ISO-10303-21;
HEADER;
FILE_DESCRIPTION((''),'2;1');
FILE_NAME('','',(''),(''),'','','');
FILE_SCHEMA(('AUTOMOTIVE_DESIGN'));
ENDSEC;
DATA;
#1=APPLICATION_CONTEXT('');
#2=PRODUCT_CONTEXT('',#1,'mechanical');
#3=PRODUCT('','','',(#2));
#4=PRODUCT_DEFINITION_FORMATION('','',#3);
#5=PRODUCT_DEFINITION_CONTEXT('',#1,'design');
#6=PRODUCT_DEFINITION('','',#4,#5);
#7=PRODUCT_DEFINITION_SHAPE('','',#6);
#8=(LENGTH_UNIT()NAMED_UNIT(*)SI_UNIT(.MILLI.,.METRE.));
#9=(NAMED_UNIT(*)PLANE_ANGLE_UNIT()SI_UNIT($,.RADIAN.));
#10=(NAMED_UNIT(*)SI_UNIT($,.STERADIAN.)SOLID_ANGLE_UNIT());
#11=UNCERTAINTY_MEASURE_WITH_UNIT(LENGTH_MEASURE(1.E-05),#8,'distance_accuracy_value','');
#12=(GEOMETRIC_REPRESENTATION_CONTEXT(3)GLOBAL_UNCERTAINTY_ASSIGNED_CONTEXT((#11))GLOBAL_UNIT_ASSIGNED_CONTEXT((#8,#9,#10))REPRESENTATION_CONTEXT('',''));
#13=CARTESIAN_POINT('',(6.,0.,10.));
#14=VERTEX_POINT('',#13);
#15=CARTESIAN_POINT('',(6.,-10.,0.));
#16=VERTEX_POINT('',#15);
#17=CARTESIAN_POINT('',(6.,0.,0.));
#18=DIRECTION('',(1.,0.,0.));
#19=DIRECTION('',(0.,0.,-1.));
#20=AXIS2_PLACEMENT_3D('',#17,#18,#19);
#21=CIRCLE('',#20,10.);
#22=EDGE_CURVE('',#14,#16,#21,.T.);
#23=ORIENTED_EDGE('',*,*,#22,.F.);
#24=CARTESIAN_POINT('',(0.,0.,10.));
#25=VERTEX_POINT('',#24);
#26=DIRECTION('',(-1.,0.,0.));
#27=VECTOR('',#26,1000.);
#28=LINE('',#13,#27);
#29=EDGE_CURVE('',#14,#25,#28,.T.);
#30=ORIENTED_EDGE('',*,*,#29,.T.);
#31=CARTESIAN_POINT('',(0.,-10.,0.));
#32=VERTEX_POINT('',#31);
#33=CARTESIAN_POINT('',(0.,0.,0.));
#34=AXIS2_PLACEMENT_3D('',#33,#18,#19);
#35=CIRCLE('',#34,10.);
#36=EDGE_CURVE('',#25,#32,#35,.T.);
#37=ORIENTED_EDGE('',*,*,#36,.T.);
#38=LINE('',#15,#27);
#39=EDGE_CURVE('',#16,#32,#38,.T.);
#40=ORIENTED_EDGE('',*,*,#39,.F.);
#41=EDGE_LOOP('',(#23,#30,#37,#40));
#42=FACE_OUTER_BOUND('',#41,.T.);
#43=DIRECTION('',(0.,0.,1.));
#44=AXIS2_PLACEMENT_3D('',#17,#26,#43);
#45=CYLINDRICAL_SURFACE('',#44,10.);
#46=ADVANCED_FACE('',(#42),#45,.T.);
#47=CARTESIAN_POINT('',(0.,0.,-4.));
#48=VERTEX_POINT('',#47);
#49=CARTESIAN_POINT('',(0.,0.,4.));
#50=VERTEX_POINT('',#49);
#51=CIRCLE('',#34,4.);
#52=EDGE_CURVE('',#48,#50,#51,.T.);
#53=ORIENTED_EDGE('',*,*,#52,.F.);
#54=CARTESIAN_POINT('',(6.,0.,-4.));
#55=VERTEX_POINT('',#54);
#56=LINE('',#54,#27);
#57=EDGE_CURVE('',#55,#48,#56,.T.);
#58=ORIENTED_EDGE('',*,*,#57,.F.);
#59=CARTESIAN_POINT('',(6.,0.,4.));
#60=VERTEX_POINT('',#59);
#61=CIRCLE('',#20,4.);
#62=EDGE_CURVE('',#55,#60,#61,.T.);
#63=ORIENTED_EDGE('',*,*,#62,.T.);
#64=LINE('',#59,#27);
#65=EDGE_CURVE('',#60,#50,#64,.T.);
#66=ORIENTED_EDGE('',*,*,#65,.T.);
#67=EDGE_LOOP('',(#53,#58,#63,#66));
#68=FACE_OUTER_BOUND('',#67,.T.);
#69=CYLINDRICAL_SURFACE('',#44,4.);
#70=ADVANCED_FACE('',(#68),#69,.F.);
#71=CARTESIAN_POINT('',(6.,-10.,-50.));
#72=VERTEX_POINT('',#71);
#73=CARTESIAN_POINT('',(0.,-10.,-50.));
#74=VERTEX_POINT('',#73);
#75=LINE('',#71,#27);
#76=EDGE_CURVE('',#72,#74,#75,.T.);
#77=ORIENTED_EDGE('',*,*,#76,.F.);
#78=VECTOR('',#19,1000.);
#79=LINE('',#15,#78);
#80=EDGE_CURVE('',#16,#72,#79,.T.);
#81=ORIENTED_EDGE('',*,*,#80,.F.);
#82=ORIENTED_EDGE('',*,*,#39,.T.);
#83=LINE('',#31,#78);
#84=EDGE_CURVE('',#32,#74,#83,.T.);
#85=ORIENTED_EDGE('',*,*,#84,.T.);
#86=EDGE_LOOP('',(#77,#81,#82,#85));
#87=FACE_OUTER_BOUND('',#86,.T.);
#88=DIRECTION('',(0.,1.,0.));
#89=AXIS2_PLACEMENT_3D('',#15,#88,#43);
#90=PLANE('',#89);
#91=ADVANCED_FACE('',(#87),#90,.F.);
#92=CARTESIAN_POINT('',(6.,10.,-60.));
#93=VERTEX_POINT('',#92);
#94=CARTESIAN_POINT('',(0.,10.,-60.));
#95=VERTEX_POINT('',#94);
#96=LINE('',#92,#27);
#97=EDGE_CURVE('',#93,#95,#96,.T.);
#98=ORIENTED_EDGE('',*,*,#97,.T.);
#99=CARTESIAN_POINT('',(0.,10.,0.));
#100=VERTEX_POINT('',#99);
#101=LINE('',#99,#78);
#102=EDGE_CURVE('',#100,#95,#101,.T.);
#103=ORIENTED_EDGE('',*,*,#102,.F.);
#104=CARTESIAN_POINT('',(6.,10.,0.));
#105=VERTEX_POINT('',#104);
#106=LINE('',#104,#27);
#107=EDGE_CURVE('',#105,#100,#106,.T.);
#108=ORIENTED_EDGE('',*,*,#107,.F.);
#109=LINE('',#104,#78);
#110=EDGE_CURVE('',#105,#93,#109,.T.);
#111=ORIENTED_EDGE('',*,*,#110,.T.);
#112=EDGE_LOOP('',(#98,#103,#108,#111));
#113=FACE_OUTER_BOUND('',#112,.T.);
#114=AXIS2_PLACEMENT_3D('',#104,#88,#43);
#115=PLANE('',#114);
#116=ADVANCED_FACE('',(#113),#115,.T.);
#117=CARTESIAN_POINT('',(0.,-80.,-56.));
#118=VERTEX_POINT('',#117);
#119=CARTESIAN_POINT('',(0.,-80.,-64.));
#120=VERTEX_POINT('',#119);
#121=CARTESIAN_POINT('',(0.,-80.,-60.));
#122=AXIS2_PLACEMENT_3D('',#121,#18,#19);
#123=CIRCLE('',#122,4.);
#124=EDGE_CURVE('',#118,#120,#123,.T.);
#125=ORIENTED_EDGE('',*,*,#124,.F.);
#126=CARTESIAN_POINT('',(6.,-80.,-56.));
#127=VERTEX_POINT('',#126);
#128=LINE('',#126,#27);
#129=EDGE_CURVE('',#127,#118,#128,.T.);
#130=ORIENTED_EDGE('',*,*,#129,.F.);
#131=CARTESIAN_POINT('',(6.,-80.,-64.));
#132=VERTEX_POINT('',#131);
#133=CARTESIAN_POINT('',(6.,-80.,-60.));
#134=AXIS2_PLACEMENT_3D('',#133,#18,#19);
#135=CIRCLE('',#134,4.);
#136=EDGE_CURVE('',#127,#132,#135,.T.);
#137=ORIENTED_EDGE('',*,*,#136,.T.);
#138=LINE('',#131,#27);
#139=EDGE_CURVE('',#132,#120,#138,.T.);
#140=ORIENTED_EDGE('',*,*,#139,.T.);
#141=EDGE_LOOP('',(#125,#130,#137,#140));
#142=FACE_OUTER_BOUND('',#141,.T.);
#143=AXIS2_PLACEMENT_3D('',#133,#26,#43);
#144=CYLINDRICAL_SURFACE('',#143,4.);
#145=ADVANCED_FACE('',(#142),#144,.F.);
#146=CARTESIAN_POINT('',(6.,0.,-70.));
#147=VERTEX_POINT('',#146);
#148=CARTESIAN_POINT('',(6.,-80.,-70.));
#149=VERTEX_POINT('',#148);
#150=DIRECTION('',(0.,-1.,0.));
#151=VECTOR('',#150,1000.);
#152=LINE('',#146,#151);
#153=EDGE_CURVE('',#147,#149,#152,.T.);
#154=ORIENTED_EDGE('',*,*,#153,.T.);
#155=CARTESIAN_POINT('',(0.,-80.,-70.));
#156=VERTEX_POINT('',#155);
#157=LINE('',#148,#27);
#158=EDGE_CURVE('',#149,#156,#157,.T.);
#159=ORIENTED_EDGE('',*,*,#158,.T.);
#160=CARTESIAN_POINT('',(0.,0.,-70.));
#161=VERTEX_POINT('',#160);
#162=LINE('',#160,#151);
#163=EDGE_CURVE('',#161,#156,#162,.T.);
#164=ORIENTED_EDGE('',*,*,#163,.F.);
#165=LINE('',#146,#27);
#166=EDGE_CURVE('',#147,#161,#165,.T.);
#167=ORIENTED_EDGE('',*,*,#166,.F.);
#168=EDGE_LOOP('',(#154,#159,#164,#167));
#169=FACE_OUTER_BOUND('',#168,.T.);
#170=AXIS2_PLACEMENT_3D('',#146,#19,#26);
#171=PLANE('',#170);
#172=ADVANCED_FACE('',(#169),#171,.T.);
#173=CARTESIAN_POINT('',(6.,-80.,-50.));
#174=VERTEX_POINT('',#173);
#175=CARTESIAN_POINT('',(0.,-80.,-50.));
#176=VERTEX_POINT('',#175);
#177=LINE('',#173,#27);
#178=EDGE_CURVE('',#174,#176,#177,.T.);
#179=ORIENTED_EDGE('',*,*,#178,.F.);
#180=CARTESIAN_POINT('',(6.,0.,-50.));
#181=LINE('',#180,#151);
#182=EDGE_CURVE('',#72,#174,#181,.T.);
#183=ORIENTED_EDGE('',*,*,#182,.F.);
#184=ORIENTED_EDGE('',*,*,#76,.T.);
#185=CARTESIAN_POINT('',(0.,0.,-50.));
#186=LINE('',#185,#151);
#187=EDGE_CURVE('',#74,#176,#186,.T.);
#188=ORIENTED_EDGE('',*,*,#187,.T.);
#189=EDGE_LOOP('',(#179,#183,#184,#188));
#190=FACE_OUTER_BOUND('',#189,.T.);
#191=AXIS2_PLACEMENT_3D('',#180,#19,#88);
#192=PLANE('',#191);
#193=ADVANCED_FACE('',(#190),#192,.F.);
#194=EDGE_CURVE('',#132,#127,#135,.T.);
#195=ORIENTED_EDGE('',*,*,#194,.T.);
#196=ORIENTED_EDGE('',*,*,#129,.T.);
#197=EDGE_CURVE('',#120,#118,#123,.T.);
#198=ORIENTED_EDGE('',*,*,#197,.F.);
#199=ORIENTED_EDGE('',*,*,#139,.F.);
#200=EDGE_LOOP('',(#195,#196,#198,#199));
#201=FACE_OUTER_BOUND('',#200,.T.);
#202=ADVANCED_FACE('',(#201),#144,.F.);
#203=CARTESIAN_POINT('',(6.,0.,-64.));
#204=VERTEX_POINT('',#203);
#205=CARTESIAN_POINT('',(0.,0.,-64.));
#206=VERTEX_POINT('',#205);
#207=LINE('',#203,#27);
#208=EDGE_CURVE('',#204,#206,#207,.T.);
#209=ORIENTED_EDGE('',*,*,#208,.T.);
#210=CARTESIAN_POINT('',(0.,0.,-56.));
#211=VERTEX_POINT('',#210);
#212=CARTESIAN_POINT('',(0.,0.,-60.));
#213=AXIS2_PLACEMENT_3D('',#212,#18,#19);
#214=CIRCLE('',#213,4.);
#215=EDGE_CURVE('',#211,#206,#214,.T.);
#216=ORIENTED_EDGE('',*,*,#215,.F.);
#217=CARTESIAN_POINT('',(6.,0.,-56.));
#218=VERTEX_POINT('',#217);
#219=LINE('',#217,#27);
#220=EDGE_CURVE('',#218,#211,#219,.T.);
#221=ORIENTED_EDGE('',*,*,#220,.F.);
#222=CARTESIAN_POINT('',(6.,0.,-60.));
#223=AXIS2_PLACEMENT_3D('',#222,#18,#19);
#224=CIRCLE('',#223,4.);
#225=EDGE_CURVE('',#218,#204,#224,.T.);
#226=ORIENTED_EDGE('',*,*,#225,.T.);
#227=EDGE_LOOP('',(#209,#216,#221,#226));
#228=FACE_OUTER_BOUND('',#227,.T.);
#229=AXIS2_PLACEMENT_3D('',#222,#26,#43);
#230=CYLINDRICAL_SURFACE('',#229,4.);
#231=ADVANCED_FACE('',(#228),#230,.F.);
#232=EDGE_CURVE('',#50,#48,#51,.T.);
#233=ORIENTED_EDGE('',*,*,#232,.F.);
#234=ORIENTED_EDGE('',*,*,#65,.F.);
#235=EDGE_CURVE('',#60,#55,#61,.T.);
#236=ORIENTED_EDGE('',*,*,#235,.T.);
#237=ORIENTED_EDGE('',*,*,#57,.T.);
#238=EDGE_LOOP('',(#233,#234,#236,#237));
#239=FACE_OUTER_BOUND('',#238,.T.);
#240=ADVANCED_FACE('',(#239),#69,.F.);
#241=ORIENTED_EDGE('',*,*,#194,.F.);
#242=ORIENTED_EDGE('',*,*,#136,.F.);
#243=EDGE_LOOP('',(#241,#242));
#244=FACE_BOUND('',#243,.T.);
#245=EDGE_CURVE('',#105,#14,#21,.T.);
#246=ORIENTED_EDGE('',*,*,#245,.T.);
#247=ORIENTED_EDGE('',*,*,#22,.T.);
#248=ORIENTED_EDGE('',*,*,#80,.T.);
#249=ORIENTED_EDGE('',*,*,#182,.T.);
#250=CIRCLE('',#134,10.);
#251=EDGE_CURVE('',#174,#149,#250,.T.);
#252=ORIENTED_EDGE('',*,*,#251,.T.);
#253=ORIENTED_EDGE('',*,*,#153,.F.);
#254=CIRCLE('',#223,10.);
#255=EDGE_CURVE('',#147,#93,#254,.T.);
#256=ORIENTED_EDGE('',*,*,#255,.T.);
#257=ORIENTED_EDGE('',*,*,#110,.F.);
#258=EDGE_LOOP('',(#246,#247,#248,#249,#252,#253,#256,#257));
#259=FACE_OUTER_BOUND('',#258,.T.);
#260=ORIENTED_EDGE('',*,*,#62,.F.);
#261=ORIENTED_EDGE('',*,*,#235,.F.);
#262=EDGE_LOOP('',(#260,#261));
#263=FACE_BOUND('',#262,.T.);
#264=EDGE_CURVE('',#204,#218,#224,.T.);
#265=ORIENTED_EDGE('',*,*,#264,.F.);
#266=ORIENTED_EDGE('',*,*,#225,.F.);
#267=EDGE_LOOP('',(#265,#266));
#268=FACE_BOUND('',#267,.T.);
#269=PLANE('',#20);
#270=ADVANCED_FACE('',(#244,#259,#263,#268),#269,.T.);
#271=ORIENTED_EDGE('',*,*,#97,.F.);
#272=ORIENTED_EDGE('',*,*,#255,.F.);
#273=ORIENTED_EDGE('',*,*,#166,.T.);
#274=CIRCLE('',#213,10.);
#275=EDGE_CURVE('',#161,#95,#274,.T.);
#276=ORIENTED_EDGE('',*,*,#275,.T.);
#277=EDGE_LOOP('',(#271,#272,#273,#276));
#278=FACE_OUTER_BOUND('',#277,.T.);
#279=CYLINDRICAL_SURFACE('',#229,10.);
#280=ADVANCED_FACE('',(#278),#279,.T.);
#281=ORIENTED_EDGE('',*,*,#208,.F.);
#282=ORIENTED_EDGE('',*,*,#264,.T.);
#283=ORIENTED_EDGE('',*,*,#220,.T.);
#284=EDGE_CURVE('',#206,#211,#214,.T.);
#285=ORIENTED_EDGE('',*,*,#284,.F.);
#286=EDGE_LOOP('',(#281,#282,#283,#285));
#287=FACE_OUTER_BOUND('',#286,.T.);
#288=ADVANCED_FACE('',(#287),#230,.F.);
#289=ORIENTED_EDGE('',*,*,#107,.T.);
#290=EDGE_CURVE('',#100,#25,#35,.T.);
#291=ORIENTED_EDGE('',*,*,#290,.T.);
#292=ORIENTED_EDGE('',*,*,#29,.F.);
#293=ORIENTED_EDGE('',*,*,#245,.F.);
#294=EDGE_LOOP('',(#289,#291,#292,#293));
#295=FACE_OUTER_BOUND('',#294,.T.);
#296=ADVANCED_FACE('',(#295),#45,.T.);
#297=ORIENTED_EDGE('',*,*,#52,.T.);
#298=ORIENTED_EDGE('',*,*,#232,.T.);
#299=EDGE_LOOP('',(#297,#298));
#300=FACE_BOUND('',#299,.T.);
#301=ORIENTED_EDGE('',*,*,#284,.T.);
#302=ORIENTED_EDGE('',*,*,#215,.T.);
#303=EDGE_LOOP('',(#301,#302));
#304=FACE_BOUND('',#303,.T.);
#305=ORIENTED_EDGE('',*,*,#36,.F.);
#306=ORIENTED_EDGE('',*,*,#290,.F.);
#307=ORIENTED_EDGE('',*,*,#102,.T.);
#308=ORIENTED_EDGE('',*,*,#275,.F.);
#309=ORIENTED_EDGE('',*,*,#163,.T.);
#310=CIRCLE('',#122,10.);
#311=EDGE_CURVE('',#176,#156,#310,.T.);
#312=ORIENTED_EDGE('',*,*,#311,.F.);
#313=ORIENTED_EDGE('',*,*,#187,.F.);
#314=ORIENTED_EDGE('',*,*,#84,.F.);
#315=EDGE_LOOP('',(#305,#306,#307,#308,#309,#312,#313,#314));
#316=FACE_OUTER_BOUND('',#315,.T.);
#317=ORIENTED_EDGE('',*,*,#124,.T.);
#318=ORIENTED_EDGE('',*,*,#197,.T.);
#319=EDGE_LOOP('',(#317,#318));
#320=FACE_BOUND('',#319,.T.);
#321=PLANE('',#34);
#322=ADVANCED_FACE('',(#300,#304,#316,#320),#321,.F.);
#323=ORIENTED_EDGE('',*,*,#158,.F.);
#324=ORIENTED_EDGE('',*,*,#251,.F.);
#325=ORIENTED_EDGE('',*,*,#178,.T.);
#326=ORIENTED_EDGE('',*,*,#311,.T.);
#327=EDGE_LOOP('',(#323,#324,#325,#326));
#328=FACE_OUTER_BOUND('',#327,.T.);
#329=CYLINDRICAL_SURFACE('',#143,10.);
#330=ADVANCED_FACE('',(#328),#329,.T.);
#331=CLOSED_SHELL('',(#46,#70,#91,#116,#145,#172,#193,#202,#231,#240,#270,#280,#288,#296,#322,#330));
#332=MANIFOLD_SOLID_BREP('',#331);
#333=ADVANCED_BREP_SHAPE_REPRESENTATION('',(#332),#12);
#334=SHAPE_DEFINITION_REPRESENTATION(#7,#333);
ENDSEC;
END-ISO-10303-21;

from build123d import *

# Parameters (mm, degrees)
SKETCH1_R           = 4
BOSS_EXTRUDE1_DEPTH = 6


with BuildPart() as part:
    # Sketch1 → Boss-Extrude1 (new body)
    # profile 1 of 3: a face of its own
    with BuildSketch(Plane(origin=(0, 0, 0), x_dir=(0, 0, -1), z_dir=(1, 0, 0))):
        with BuildLine():
            Line((60, 10), (0, 10))
            ThreePointArc((0, 10), (-10, 0), (0, -10))
            Line((0, -10), (50, -10))
            Line((50, -10), (50, 0))
            ThreePointArc((50, 0), (52.928932188, 7.071067812), (60, 10))
        make_face()
        Circle(SKETCH1_R, mode=Mode.SUBTRACT)
    # profile 2 of 3: a face of its own
    with BuildSketch(Plane(origin=(0, 0, 0), x_dir=(0, 0, -1), z_dir=(1, 0, 0))):
        with BuildLine():
            ThreePointArc((70, 0), (67.071067812, 7.071067812), (60, 10))
            ThreePointArc((60, 10), (52.928932188, 7.071067812), (50, 0))
            Line((50, 0), (50, -10))
            Line((50, -10), (60, -10))
            ThreePointArc((60, -10), (67.071067812, -7.071067812), (70, 0))
        make_face()
        with Locations((60, 0)):
            Circle(SKETCH1_R, mode=Mode.SUBTRACT)
    # profile 3 of 3: a face of its own
    with BuildSketch(Plane(origin=(0, 0, 0), x_dir=(0, 0, -1), z_dir=(1, 0, 0))):
        with BuildLine():
            Line((70, -80), (70, 0))
            ThreePointArc((70, 0), (67.071067812, -7.071067812), (60, -10))
            Line((60, -10), (50, -10))
            Line((50, -10), (50, -80))
            ThreePointArc((50, -80), (60, -90), (70, -80))
        make_face()
        with Locations((60, -80)):
            Circle(SKETCH1_R, mode=Mode.SUBTRACT)
    extrude(amount=BOSS_EXTRUDE1_DEPTH)


solid = part.part
